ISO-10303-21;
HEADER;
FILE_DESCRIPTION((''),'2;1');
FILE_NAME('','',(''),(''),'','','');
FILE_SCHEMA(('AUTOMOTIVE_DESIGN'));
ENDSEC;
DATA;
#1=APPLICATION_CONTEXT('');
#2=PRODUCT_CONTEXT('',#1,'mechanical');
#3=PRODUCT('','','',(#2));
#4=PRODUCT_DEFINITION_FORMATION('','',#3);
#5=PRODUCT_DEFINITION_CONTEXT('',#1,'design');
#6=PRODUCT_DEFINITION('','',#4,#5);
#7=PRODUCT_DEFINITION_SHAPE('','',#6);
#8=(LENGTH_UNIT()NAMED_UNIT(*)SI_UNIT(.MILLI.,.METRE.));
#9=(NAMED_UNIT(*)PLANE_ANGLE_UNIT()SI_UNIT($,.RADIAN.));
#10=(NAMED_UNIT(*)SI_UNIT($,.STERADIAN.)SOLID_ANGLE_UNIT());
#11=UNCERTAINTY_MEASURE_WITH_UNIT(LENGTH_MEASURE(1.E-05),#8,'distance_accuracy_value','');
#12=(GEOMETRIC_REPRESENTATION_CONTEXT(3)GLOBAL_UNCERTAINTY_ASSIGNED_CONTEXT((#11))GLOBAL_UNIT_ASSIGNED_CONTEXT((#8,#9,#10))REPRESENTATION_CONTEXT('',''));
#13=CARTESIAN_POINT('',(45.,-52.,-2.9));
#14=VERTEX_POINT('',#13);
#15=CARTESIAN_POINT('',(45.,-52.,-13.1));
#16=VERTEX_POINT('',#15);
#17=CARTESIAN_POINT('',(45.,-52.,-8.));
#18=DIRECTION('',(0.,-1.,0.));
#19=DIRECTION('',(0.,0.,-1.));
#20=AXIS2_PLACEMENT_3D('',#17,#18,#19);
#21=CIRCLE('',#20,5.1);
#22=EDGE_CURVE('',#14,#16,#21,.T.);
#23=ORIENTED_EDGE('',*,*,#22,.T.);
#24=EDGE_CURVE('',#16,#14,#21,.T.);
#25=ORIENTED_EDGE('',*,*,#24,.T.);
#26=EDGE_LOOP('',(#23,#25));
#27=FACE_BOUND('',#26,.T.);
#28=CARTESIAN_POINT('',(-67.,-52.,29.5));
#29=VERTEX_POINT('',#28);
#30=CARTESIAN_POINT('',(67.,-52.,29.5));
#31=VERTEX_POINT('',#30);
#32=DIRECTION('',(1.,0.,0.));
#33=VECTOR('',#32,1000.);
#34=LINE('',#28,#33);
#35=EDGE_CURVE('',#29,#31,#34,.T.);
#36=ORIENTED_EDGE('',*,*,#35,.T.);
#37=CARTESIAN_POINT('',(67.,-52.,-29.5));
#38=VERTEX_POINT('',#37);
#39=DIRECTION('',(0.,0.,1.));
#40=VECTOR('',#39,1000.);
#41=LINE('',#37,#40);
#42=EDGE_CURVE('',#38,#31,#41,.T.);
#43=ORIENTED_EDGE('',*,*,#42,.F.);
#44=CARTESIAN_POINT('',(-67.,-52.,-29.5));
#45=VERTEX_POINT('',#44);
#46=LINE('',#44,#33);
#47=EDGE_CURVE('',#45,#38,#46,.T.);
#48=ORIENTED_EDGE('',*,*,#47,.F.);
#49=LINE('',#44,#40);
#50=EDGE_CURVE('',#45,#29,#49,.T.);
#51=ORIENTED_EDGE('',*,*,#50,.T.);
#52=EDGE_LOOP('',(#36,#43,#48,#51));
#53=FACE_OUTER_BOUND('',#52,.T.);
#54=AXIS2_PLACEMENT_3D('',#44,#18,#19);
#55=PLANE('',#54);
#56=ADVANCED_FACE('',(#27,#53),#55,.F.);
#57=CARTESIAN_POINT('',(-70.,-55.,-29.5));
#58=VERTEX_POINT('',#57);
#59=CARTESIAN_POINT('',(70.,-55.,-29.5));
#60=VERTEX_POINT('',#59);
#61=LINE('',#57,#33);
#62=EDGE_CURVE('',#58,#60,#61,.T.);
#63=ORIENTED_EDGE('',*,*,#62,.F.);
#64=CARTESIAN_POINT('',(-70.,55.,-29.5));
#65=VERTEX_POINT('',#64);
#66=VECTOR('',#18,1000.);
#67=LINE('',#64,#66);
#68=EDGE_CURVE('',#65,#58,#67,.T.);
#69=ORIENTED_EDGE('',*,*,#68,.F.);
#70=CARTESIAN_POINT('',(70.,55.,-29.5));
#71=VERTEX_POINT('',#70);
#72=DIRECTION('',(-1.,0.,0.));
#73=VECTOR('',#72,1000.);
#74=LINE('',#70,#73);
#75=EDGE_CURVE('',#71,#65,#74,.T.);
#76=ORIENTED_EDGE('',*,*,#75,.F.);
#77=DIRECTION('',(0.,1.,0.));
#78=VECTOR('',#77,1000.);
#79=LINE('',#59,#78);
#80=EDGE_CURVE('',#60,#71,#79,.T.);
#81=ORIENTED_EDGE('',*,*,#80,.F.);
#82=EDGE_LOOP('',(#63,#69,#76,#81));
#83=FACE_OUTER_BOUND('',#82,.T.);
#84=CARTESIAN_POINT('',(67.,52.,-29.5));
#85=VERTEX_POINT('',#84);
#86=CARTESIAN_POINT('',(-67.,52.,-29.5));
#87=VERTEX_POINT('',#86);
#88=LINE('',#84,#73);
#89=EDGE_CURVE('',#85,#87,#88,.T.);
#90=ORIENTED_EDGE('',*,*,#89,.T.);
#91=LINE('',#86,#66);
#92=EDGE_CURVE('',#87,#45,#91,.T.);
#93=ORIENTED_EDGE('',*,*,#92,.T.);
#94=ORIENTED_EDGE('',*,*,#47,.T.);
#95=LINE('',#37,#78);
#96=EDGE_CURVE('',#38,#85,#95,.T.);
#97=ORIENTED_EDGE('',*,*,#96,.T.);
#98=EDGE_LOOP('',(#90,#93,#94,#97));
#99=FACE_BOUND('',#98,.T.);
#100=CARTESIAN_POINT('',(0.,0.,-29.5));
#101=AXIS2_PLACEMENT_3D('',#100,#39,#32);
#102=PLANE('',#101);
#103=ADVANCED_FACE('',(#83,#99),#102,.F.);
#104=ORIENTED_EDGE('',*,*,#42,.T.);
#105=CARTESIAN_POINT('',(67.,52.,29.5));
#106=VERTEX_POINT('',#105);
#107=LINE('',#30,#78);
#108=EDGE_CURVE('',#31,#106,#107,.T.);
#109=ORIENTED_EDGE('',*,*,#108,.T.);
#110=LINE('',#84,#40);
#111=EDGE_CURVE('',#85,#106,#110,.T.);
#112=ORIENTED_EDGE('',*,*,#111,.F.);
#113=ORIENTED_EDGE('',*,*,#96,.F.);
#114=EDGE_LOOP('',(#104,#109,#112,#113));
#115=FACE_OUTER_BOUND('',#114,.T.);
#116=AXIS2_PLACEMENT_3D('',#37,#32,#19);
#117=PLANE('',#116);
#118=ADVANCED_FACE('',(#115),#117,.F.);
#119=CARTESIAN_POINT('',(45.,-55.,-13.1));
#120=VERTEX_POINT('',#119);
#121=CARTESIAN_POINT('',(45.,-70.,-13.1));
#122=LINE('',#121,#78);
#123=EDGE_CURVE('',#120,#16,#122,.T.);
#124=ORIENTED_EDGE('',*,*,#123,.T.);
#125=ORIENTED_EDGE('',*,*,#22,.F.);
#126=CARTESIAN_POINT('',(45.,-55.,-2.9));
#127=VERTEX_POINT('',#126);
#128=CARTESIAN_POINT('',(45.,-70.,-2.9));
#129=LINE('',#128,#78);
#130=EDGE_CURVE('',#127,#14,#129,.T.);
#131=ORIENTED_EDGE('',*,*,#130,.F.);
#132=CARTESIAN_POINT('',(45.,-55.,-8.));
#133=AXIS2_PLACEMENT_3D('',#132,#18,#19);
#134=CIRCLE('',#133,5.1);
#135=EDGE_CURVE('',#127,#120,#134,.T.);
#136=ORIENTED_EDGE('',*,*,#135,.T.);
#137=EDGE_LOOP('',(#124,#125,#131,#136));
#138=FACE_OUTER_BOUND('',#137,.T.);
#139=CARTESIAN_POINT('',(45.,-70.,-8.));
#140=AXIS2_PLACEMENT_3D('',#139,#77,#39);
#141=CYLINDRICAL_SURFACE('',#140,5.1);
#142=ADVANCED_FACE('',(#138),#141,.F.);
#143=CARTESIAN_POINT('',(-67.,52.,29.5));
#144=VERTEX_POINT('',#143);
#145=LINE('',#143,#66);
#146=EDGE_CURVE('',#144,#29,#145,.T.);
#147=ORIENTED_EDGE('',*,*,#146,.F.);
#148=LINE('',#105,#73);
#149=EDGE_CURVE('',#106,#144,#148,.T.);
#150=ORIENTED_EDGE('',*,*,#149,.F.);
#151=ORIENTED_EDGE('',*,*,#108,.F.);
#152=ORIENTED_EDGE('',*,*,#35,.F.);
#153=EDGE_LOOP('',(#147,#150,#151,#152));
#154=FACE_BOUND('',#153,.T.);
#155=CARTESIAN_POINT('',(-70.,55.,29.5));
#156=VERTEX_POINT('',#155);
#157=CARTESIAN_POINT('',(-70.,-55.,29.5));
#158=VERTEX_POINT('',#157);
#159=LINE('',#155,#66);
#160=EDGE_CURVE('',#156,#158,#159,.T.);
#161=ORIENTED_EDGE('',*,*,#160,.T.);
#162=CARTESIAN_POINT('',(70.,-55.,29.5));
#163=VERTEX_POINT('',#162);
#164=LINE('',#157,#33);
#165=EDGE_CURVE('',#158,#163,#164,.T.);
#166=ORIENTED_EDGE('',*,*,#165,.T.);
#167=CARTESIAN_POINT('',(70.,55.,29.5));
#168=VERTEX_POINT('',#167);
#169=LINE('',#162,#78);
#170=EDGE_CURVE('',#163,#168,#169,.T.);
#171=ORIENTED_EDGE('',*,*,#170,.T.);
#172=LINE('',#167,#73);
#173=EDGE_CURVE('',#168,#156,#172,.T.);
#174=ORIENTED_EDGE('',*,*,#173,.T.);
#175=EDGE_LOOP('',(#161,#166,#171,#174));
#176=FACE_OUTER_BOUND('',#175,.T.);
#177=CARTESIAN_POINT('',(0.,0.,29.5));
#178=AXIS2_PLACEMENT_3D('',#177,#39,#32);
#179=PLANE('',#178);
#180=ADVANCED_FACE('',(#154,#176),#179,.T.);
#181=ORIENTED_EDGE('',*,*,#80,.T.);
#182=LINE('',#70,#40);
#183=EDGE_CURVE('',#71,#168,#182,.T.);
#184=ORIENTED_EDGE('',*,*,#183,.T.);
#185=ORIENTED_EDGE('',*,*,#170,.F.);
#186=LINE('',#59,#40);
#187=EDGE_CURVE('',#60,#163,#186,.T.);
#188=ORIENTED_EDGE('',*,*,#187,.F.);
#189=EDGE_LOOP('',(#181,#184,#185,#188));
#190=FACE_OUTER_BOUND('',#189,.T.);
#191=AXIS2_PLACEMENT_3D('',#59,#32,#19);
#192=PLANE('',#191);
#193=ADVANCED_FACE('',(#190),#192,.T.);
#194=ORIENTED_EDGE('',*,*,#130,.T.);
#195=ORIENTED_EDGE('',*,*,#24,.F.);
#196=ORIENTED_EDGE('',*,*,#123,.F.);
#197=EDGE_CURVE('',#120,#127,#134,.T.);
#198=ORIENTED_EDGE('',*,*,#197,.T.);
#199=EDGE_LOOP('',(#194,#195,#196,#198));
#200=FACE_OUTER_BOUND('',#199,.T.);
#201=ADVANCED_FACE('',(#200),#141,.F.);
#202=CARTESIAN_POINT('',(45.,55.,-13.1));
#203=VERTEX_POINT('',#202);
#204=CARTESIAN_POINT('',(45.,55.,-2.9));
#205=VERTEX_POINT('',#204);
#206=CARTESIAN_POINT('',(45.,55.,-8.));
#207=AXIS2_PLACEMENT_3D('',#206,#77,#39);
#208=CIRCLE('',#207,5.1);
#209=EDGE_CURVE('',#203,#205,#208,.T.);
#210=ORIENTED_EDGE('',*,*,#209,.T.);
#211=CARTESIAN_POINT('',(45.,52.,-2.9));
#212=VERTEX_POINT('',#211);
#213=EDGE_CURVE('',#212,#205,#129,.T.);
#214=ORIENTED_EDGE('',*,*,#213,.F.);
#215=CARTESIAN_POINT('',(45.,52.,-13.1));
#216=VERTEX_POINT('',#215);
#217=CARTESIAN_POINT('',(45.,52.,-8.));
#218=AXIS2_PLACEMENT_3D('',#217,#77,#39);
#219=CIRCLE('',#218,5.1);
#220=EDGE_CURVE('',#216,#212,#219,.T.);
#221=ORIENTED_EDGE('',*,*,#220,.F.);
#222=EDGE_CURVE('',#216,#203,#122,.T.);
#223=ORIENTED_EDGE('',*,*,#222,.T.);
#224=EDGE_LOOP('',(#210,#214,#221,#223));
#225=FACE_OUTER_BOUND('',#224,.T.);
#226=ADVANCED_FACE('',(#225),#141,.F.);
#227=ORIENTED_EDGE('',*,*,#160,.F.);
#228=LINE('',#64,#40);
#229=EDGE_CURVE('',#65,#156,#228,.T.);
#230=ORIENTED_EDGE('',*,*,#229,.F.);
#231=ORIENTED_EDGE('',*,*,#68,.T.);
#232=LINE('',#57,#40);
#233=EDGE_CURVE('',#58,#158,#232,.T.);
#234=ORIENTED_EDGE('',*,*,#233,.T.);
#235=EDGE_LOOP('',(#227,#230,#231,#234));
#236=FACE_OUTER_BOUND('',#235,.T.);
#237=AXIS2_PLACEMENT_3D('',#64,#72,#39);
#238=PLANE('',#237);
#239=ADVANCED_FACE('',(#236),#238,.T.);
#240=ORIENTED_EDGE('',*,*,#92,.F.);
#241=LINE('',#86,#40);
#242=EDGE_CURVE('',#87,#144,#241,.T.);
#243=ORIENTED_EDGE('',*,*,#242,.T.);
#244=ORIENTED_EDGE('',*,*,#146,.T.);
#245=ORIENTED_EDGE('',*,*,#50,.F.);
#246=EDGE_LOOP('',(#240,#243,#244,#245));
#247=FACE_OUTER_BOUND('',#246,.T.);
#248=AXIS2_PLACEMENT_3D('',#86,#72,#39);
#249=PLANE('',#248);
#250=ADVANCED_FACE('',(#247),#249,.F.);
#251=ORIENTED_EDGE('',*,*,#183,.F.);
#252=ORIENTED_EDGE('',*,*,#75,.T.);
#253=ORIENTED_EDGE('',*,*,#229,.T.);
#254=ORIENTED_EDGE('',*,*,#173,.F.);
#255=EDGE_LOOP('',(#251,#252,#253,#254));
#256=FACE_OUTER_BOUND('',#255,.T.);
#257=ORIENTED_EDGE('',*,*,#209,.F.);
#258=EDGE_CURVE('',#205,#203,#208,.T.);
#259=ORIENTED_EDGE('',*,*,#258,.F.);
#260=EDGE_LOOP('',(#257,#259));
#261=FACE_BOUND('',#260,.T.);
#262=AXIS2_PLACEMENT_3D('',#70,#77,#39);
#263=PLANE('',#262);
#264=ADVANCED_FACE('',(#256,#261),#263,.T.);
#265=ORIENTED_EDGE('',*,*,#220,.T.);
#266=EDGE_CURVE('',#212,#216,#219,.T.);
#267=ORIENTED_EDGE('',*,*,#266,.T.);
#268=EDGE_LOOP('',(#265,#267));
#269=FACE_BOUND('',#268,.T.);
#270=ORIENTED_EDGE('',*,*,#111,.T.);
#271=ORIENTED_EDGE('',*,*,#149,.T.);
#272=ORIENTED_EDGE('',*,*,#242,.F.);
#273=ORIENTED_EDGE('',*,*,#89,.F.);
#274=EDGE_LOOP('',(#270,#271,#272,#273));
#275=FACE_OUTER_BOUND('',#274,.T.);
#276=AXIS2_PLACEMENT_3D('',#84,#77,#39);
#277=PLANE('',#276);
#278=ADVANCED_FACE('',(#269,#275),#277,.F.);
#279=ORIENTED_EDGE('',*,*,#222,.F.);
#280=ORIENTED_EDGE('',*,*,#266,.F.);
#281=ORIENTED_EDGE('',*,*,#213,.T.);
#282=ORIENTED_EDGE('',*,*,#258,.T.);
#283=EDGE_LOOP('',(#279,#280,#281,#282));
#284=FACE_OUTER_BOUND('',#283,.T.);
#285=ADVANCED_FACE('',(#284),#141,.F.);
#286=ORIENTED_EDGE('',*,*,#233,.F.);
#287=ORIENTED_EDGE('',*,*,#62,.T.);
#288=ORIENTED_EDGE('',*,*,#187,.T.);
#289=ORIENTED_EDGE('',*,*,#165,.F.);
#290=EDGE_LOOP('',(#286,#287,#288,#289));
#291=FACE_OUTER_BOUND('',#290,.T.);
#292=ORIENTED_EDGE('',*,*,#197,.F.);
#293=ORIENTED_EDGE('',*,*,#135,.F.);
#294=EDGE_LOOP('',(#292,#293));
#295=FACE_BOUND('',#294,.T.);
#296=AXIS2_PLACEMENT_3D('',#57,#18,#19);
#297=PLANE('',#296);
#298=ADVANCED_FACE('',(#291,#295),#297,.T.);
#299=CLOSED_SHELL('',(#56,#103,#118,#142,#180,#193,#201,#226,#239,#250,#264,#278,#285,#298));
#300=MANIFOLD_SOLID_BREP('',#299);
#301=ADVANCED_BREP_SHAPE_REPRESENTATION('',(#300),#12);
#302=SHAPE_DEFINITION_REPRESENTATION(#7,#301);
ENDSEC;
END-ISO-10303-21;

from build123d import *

# Parameters (mm, degrees)
SKETCH_1_W          = 140
SKETCH_1_H          = 110
SKETCH_1_W_2        = 134
SKETCH_1_H_2        = 104
EXTRUDE_1_DEPTH     = 29.5
SKETCH_2_R          = 5.1
CUT_EXTRUDE_1_DEPTH = 70


with BuildPart() as part:
    # 草图1 → 凸台-拉伸1 (new, symmetric)
    with BuildSketch(Plane.XY):
        Rectangle(SKETCH_1_W, SKETCH_1_H)
        Rectangle(SKETCH_1_W_2, SKETCH_1_H_2, mode=Mode.SUBTRACT)
    extrude(amount=EXTRUDE_1_DEPTH, both=True)

    # 草图2 → 切除-拉伸1 (cut, symmetric)
    with BuildSketch(Plane(origin=(0, 0, 0), x_dir=(1, 0, 0), z_dir=(0, 1, 0))):
        with Locations(Location((45, 8, 0), (0, 0, 90))):
            Circle(SKETCH_2_R)
    extrude(amount=CUT_EXTRUDE_1_DEPTH, both=True, mode=Mode.SUBTRACT)


solid = part.part
